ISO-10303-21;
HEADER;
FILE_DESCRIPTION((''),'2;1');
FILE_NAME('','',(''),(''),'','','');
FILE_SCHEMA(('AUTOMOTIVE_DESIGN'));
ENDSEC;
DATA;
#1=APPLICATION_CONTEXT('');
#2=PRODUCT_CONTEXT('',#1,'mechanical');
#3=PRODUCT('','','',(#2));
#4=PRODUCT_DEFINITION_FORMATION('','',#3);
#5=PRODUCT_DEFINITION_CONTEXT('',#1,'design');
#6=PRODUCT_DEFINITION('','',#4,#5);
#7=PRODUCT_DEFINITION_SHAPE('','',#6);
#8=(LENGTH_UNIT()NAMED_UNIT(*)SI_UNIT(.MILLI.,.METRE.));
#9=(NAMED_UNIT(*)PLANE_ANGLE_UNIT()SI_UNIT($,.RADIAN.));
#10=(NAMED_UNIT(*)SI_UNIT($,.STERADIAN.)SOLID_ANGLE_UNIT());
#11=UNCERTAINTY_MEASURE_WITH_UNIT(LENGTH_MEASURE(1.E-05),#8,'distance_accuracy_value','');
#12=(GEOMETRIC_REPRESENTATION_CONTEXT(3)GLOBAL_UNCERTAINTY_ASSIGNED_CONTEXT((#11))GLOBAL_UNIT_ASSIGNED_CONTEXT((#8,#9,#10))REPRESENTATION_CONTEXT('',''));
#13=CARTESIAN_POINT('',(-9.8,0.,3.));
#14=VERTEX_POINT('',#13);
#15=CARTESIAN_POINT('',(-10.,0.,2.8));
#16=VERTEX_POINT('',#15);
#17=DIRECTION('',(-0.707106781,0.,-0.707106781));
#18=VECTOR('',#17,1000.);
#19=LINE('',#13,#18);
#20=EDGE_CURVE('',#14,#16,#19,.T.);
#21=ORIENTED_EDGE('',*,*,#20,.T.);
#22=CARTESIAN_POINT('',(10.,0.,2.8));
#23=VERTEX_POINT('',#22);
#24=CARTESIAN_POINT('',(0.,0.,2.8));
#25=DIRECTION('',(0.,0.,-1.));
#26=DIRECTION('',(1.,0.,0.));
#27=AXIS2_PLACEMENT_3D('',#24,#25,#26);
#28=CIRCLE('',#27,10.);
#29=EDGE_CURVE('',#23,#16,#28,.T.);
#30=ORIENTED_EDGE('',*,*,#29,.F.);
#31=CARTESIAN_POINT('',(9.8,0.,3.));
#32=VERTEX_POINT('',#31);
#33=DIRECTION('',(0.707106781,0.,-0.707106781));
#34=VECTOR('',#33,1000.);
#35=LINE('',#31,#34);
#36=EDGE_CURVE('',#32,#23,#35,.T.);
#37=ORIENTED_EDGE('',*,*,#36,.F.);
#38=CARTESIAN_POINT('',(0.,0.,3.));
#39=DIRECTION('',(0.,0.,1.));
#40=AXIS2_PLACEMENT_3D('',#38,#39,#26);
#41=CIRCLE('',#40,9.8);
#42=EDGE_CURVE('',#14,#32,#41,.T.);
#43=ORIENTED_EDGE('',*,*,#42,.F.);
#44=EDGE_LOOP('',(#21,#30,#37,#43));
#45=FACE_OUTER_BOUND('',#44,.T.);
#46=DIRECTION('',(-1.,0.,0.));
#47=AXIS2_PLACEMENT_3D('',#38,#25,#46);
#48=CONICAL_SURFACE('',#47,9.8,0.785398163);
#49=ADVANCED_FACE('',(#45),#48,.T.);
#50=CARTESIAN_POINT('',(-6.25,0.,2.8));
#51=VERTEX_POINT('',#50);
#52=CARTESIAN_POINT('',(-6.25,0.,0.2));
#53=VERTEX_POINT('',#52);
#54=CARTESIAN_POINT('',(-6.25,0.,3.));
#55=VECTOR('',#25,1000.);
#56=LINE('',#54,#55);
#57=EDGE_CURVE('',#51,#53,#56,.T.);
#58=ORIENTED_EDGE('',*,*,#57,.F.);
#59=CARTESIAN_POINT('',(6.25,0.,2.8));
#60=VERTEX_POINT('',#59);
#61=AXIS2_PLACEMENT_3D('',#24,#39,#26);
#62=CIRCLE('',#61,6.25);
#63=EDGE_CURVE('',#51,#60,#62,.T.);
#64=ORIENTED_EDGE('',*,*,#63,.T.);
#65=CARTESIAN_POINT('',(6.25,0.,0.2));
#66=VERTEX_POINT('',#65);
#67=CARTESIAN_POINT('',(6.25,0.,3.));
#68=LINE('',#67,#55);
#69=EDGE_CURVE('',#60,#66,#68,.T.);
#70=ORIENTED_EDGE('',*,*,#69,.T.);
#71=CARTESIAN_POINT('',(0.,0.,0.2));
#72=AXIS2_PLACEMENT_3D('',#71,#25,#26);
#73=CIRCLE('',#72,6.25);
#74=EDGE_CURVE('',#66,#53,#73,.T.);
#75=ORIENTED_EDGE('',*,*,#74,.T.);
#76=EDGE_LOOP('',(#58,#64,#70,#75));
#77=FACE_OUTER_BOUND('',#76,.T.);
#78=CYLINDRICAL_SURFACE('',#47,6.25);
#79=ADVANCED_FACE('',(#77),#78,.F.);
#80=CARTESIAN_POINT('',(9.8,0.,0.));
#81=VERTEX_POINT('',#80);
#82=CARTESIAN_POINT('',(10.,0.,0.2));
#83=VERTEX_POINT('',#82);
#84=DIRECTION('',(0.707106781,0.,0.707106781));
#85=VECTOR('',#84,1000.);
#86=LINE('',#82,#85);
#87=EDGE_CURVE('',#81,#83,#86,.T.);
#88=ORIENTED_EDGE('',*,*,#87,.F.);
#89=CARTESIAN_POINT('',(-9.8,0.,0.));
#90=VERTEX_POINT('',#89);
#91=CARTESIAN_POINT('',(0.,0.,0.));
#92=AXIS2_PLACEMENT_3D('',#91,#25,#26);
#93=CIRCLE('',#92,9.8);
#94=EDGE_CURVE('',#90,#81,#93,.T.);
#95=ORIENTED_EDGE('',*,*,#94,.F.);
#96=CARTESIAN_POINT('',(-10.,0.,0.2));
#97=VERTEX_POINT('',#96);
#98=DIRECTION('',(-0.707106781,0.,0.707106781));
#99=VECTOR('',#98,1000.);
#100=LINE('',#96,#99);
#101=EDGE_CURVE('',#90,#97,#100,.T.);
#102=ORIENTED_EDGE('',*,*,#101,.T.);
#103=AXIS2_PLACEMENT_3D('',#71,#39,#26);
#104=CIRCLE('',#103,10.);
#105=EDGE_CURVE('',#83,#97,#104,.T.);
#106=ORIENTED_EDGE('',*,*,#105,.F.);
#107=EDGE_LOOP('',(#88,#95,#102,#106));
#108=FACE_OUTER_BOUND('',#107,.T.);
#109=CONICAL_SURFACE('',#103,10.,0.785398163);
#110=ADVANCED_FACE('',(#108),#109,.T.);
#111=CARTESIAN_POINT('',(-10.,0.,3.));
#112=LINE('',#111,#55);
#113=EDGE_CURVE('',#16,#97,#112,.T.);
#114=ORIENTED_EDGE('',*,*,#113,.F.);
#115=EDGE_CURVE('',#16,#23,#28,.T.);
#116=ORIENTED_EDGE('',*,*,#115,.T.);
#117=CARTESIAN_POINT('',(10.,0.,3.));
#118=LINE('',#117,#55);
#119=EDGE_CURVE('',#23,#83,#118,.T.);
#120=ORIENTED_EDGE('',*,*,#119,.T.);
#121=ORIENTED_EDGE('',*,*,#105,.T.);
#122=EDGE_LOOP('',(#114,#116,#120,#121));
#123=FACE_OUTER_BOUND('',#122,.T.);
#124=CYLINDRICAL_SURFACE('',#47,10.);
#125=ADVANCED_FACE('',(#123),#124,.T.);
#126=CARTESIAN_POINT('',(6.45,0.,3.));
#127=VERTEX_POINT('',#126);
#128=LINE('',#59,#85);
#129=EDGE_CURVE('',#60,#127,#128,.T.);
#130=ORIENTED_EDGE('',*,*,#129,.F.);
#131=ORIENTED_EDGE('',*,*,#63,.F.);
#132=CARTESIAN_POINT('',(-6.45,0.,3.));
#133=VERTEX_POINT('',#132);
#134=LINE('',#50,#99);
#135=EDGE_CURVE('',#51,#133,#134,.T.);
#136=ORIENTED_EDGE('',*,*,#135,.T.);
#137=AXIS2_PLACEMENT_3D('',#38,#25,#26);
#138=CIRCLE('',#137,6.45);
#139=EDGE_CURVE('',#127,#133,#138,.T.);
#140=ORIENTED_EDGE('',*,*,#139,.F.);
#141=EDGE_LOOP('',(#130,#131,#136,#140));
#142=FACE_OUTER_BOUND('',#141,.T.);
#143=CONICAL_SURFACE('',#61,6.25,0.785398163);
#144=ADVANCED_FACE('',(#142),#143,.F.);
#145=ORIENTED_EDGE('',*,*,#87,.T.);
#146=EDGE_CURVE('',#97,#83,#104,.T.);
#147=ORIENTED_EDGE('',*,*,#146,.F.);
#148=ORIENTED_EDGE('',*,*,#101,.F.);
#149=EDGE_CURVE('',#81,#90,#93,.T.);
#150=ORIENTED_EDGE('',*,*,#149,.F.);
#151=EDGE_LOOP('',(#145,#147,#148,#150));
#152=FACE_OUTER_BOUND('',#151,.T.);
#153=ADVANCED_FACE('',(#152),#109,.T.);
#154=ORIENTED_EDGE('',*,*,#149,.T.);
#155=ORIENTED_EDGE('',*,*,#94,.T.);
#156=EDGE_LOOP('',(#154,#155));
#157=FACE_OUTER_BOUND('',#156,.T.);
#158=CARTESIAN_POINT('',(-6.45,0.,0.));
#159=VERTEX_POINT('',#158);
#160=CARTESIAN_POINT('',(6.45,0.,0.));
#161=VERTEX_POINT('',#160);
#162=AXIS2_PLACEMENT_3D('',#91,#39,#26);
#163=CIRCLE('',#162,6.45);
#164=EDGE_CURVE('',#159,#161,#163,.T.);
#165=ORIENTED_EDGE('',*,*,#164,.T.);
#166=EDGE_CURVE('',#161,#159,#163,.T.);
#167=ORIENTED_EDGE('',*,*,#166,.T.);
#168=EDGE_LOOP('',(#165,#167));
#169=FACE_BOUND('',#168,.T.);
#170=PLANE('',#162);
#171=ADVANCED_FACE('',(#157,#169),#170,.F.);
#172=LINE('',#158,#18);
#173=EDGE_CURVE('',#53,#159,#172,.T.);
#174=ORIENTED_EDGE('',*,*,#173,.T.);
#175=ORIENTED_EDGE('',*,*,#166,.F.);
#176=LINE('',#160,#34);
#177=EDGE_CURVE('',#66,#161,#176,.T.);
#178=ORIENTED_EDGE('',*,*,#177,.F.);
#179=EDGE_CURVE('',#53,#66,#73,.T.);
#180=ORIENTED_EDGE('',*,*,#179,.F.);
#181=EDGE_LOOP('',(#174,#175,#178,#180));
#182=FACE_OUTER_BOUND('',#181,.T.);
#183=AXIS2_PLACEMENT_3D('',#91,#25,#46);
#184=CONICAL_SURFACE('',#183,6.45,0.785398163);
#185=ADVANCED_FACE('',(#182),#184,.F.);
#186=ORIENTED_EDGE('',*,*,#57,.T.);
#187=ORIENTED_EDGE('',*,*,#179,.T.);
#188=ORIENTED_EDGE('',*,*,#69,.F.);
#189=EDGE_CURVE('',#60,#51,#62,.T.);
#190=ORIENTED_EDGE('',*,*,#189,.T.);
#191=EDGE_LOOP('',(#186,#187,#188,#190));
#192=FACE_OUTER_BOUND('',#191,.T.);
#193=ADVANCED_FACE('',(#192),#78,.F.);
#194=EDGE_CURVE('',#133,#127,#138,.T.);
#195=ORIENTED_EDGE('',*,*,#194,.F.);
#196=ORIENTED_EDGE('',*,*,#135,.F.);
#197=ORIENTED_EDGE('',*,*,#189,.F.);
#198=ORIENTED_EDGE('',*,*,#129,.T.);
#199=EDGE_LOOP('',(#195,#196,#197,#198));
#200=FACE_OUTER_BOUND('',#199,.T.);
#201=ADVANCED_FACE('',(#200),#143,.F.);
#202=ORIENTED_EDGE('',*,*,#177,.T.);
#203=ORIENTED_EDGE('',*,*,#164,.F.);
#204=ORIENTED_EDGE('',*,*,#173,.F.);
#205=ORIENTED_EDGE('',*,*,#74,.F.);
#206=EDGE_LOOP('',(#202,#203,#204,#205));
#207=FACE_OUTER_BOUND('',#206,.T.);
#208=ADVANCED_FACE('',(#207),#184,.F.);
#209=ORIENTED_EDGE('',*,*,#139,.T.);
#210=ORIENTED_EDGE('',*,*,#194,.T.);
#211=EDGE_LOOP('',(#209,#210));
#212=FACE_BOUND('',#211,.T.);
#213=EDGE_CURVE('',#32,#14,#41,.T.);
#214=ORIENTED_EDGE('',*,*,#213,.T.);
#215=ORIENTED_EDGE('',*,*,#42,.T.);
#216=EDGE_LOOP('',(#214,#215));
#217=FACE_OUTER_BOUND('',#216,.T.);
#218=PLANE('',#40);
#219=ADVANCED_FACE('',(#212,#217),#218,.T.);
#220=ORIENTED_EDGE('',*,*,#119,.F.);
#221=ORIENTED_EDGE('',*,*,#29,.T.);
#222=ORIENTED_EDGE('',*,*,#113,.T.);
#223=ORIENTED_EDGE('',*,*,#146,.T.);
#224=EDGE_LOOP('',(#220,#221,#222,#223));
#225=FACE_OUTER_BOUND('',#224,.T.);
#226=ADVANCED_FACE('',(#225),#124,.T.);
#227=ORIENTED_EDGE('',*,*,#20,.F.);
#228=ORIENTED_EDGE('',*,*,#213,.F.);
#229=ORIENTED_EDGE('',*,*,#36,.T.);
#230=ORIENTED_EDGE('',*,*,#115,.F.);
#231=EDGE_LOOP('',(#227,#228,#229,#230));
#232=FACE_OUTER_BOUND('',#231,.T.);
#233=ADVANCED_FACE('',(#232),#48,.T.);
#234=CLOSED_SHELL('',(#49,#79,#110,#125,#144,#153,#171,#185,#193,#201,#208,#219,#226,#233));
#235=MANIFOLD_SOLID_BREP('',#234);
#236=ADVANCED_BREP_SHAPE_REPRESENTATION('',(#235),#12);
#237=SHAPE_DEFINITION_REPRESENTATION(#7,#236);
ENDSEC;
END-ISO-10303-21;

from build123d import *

# Parameters (mm, degrees)
SKETCH1_R           = 10
SKETCH1_R_2         = 6.25
BOSS_EXTRUDE1_DEPTH = 3
CHAMFER1_SIZE       = 0.2


with BuildPart() as part:
    # Sketch1 → Boss-Extrude1 (new body)
    with BuildSketch(Plane.XY):
        Circle(SKETCH1_R)
        Circle(SKETCH1_R_2, mode=Mode.SUBTRACT)
    extrude(amount=BOSS_EXTRUDE1_DEPTH)

    # Chamfer1
    chamfer1_edges = [part.edges().sort_by_distance(p)[0] for p in [
        (-10, 0, 0),
        (-10, 0, 3),
        (-6.25, 0, 0),
        (-6.25, 0, 3),
    ]]
    chamfer(chamfer1_edges, length=CHAMFER1_SIZE)


solid = part.part
